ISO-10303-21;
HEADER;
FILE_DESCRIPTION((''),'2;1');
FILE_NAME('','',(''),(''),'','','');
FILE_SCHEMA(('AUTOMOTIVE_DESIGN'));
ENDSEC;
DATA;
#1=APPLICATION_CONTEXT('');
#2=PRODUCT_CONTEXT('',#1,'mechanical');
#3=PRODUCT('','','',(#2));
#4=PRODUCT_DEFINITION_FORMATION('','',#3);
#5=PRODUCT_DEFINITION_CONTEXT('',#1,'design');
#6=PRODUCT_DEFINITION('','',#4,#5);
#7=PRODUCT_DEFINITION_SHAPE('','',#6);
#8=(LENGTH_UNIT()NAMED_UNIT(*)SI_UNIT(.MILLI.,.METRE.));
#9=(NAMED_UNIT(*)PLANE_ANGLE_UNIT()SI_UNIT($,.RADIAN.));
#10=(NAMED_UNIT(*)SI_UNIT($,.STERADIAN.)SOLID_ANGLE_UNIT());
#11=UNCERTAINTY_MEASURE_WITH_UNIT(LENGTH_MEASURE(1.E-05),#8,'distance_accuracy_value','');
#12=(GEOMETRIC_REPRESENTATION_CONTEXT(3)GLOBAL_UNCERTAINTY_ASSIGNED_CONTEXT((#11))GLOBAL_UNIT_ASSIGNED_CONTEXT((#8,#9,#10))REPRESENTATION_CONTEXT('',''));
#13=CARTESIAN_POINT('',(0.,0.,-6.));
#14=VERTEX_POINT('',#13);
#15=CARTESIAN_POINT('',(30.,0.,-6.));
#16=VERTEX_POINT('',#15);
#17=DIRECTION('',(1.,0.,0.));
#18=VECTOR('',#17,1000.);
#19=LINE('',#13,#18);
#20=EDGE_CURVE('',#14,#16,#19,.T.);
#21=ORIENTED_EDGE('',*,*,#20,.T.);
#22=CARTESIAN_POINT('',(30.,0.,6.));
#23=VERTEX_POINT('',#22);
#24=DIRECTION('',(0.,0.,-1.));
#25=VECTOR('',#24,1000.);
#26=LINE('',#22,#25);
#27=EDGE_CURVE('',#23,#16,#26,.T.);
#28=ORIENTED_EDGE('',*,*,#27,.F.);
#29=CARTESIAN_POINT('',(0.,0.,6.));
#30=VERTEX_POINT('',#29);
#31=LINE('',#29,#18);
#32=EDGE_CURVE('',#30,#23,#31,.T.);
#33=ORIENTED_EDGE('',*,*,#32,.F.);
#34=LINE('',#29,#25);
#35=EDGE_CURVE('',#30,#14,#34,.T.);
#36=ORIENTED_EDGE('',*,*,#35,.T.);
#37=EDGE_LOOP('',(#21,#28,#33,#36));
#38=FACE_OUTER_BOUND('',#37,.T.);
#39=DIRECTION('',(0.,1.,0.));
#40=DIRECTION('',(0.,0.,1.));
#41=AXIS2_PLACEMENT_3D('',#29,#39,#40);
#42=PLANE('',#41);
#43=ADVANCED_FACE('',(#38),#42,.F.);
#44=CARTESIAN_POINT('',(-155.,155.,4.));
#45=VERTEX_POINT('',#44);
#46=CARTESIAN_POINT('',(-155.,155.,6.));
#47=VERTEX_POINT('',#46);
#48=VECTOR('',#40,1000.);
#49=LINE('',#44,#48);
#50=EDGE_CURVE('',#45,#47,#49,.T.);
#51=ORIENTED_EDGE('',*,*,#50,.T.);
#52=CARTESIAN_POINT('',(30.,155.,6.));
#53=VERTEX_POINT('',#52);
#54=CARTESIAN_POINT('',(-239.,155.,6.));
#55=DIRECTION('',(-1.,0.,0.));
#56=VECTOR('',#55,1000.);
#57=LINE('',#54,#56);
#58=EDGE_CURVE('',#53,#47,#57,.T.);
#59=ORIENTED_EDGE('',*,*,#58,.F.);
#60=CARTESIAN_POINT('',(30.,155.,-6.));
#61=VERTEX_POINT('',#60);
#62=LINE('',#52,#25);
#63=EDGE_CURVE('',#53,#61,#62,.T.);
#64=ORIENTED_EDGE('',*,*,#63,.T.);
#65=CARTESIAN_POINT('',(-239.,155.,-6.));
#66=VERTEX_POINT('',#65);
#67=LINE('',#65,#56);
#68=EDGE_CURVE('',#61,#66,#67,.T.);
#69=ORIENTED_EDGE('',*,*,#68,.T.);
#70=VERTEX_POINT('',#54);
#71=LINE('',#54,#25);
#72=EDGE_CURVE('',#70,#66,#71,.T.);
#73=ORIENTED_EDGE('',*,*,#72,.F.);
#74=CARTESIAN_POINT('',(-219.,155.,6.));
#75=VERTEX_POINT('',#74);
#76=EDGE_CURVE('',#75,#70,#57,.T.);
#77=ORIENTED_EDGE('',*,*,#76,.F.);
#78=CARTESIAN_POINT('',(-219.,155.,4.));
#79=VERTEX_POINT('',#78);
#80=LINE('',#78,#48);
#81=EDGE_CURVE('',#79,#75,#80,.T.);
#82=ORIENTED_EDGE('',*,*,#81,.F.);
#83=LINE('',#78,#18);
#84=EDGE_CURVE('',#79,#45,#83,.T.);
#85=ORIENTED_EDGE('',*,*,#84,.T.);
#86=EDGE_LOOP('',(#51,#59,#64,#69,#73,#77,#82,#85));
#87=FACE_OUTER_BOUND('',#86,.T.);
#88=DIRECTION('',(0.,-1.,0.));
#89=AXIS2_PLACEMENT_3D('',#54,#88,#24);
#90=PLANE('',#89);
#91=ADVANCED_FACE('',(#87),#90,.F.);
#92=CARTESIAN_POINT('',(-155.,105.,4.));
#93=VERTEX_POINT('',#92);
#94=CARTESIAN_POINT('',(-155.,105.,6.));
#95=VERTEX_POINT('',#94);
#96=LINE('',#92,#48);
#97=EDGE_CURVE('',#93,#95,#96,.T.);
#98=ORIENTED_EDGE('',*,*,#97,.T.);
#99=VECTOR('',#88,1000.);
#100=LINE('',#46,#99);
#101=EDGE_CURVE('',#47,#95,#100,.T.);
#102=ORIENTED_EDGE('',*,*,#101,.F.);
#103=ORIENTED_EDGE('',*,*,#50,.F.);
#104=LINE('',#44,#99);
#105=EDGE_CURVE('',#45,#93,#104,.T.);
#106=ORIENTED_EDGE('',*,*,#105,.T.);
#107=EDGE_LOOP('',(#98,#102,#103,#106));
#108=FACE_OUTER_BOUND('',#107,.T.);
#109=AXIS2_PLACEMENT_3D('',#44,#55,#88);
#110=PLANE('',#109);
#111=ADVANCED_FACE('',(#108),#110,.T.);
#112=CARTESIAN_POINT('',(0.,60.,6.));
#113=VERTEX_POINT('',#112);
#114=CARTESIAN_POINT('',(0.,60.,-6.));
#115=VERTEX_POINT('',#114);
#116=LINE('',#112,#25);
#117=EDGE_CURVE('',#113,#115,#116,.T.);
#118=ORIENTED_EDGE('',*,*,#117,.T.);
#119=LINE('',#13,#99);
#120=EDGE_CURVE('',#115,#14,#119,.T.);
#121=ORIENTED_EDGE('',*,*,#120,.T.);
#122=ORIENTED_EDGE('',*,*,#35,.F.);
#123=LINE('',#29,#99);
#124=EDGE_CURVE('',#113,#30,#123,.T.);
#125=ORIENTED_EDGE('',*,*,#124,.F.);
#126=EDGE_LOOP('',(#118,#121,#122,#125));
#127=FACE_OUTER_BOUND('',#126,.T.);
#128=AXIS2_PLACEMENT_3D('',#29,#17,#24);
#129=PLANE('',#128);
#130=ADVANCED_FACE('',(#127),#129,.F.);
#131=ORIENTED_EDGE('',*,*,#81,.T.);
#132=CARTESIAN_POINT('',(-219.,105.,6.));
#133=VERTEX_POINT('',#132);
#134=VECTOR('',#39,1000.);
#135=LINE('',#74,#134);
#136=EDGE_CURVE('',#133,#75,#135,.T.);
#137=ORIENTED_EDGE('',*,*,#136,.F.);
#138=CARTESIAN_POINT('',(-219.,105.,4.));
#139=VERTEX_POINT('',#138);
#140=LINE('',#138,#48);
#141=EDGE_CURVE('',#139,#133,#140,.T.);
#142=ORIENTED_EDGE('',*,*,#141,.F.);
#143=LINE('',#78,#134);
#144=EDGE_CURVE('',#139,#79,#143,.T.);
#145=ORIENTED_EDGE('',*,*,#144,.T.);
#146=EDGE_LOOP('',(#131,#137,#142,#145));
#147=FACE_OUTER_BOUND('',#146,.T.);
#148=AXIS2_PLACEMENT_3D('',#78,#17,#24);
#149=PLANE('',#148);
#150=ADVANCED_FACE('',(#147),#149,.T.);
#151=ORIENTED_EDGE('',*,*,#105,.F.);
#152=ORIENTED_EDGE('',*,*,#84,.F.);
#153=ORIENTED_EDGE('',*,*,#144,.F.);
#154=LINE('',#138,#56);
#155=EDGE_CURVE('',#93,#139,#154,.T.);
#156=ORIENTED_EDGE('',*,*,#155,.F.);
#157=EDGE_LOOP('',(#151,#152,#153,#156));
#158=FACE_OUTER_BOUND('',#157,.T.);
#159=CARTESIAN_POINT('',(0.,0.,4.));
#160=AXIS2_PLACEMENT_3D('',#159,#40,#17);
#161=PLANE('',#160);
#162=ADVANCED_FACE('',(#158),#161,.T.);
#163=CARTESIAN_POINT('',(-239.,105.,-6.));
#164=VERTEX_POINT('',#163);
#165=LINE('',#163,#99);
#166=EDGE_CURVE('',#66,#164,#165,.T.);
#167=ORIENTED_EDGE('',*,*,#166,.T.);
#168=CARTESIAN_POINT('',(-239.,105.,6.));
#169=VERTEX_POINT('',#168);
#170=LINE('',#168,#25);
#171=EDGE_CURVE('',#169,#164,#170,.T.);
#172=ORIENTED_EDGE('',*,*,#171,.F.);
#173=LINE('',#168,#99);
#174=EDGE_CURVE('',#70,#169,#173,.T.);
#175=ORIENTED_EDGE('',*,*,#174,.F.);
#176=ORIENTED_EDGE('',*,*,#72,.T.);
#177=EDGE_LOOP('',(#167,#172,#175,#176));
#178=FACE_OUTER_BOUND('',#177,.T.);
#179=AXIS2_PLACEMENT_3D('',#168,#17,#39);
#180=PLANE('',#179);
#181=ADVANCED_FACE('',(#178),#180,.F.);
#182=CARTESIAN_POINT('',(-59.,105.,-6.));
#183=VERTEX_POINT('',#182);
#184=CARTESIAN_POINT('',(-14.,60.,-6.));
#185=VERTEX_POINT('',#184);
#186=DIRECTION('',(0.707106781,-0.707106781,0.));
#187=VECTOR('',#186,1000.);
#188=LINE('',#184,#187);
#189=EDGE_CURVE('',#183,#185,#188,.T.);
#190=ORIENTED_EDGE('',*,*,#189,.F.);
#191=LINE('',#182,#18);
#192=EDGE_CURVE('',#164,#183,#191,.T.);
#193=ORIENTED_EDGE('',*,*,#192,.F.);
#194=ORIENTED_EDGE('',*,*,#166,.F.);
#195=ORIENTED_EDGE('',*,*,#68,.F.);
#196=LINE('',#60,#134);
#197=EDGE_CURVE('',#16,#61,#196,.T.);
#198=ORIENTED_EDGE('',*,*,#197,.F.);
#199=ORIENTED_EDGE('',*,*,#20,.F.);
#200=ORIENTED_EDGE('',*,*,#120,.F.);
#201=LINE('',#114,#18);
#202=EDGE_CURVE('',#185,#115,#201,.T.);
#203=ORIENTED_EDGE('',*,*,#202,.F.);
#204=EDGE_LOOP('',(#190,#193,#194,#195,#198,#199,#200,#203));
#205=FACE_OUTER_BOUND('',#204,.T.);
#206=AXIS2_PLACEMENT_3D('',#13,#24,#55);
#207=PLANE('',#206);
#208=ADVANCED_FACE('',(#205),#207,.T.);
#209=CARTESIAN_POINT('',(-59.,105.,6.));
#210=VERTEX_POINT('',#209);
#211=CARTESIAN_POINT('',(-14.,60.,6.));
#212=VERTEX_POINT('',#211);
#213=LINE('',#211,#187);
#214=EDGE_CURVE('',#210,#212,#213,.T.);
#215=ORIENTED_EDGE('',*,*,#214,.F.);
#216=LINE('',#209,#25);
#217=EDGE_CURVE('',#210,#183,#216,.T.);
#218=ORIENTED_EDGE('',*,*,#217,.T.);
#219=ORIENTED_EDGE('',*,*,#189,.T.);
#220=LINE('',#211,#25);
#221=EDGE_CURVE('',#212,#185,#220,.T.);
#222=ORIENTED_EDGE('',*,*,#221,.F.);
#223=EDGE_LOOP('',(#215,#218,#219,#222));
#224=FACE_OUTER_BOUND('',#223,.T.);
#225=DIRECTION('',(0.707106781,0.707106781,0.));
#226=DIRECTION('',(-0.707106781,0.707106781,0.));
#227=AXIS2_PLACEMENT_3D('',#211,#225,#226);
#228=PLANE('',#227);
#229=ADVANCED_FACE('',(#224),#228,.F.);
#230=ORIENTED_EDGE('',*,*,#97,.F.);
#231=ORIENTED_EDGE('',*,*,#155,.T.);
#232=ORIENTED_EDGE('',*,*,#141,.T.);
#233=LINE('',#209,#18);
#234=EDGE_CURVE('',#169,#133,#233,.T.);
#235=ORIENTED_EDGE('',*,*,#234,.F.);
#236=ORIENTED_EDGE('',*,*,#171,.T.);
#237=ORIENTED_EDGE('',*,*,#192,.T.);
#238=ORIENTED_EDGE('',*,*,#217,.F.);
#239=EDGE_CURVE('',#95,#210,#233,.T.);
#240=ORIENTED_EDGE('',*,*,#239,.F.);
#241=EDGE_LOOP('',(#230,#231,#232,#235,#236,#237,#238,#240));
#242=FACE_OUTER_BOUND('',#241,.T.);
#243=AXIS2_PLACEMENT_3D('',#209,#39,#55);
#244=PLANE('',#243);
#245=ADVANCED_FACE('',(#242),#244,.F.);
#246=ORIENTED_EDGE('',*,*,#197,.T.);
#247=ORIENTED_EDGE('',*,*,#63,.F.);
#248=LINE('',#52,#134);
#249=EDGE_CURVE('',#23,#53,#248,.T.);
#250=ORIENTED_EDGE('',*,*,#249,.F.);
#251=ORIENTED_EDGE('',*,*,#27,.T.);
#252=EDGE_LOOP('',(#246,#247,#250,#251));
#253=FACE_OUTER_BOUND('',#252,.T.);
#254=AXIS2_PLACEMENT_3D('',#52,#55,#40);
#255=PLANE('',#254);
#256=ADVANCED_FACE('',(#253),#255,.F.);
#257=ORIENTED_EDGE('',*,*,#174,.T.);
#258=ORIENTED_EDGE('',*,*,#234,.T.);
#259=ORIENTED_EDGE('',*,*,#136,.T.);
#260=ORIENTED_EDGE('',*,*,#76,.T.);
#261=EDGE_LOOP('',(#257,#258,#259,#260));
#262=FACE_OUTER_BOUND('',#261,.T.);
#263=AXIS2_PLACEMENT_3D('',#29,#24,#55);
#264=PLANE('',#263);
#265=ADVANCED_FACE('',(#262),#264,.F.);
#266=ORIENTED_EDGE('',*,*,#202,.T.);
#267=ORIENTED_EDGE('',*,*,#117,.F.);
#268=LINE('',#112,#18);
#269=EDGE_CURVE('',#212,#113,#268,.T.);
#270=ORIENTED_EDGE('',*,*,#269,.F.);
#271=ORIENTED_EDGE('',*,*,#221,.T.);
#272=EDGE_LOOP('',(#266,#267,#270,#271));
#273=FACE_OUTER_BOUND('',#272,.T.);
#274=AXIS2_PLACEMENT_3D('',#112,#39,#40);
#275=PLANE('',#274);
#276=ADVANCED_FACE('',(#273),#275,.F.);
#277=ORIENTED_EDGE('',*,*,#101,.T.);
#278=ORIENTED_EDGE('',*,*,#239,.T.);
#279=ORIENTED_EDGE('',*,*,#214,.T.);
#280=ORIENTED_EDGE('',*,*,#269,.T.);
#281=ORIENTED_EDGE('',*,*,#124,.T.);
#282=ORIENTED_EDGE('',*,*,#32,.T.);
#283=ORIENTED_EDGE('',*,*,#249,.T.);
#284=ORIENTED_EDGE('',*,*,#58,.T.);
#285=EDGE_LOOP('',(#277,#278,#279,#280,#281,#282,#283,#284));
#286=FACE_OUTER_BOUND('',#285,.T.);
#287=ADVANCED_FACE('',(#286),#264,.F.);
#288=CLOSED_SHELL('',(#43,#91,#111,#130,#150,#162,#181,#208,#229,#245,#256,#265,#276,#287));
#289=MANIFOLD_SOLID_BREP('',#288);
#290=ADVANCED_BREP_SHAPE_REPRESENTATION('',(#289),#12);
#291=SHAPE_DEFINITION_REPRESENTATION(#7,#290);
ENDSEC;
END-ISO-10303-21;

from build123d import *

# Parameters (mm, degrees)
EXTRUDE_1_DEPTH     = 6
SKETCH_2_W          = 64
SKETCH_2_H          = 50
CUT_EXTRUDE_1_DEPTH = 2


with BuildPart() as part:
    # 草图1 → 凸台-拉伸1 (new, symmetric)
    with BuildSketch(Plane.XY):
        Polygon((0, 0), (0, 60), (-14, 60), (-59, 105), (-239, 105), (-239, 155), (30, 155), (30, 0), align=None)
    extrude(amount=EXTRUDE_1_DEPTH, both=True)

    # 草图2 → 切除-拉伸1 (cut)
    with BuildSketch(Plane(origin=(0, 0, 6), x_dir=(-1, 0, 0), z_dir=(0, 0, -1))):
        with Locations((187, 130)):
            Rectangle(SKETCH_2_W, SKETCH_2_H)
    extrude(amount=CUT_EXTRUDE_1_DEPTH, mode=Mode.SUBTRACT)


solid = part.part
